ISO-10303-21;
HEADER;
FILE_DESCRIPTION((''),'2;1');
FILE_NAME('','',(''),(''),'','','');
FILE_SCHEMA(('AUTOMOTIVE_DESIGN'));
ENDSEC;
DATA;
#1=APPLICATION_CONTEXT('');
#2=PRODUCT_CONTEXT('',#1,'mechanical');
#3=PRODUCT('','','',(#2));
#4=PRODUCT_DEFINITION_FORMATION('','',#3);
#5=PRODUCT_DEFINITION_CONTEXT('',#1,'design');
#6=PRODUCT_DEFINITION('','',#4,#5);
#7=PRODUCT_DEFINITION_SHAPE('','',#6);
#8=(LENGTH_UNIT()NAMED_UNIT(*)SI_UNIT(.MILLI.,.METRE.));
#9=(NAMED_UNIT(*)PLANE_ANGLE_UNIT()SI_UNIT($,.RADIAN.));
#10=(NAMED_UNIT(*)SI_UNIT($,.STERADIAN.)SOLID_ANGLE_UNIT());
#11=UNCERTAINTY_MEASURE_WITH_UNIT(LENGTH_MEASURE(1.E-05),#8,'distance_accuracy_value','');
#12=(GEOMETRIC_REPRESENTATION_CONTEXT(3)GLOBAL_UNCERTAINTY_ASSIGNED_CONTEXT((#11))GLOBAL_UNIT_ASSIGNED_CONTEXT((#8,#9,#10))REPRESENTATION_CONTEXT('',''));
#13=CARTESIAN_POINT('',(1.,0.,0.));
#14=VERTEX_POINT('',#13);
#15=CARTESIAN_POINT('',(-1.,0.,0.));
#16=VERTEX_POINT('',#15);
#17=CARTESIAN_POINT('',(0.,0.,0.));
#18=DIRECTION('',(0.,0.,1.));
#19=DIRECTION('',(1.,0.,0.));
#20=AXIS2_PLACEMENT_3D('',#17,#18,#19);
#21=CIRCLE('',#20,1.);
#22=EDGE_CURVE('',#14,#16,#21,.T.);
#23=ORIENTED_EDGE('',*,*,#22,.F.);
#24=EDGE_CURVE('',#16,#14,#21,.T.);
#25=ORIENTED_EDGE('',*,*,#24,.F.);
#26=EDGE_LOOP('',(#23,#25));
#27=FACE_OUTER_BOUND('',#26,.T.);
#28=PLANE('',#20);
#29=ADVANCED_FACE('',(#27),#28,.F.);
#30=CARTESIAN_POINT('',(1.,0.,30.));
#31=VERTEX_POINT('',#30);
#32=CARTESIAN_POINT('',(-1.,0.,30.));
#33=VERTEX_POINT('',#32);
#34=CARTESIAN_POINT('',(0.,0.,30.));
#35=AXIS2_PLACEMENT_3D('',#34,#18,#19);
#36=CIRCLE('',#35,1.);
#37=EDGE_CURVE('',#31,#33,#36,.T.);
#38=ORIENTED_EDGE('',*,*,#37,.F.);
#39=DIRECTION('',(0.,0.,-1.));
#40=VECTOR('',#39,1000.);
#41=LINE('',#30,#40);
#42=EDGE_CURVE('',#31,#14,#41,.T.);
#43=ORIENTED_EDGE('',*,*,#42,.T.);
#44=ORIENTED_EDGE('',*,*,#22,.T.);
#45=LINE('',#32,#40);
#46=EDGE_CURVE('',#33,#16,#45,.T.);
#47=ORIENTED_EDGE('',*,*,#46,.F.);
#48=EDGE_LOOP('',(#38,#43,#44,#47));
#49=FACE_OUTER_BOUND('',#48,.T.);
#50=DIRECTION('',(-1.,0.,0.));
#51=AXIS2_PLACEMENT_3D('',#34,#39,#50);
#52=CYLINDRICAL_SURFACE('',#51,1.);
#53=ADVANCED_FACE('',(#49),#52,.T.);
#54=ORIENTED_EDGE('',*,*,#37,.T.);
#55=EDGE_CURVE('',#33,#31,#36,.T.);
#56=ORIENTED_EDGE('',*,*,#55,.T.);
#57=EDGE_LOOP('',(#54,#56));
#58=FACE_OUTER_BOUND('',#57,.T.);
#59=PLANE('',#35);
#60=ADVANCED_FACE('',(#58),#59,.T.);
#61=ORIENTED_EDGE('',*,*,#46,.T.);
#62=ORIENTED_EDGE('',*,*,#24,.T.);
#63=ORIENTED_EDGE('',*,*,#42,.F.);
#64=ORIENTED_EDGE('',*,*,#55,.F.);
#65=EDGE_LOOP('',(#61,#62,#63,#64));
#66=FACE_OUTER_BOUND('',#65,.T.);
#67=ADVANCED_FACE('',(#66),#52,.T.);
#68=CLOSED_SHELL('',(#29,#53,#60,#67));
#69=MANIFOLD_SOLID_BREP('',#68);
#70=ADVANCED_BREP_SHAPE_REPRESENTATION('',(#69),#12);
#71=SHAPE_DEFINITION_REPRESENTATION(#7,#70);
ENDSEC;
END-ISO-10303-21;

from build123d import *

# Parameters (mm, degrees)
SKETCH1_R           = 1
BOSS_EXTRUDE1_DEPTH = 30


with BuildPart() as part:
    # Sketch1 → Boss-Extrude1 (new body)
    with BuildSketch(Plane.XY):
        Circle(SKETCH1_R)
    extrude(amount=BOSS_EXTRUDE1_DEPTH)


solid = part.part
